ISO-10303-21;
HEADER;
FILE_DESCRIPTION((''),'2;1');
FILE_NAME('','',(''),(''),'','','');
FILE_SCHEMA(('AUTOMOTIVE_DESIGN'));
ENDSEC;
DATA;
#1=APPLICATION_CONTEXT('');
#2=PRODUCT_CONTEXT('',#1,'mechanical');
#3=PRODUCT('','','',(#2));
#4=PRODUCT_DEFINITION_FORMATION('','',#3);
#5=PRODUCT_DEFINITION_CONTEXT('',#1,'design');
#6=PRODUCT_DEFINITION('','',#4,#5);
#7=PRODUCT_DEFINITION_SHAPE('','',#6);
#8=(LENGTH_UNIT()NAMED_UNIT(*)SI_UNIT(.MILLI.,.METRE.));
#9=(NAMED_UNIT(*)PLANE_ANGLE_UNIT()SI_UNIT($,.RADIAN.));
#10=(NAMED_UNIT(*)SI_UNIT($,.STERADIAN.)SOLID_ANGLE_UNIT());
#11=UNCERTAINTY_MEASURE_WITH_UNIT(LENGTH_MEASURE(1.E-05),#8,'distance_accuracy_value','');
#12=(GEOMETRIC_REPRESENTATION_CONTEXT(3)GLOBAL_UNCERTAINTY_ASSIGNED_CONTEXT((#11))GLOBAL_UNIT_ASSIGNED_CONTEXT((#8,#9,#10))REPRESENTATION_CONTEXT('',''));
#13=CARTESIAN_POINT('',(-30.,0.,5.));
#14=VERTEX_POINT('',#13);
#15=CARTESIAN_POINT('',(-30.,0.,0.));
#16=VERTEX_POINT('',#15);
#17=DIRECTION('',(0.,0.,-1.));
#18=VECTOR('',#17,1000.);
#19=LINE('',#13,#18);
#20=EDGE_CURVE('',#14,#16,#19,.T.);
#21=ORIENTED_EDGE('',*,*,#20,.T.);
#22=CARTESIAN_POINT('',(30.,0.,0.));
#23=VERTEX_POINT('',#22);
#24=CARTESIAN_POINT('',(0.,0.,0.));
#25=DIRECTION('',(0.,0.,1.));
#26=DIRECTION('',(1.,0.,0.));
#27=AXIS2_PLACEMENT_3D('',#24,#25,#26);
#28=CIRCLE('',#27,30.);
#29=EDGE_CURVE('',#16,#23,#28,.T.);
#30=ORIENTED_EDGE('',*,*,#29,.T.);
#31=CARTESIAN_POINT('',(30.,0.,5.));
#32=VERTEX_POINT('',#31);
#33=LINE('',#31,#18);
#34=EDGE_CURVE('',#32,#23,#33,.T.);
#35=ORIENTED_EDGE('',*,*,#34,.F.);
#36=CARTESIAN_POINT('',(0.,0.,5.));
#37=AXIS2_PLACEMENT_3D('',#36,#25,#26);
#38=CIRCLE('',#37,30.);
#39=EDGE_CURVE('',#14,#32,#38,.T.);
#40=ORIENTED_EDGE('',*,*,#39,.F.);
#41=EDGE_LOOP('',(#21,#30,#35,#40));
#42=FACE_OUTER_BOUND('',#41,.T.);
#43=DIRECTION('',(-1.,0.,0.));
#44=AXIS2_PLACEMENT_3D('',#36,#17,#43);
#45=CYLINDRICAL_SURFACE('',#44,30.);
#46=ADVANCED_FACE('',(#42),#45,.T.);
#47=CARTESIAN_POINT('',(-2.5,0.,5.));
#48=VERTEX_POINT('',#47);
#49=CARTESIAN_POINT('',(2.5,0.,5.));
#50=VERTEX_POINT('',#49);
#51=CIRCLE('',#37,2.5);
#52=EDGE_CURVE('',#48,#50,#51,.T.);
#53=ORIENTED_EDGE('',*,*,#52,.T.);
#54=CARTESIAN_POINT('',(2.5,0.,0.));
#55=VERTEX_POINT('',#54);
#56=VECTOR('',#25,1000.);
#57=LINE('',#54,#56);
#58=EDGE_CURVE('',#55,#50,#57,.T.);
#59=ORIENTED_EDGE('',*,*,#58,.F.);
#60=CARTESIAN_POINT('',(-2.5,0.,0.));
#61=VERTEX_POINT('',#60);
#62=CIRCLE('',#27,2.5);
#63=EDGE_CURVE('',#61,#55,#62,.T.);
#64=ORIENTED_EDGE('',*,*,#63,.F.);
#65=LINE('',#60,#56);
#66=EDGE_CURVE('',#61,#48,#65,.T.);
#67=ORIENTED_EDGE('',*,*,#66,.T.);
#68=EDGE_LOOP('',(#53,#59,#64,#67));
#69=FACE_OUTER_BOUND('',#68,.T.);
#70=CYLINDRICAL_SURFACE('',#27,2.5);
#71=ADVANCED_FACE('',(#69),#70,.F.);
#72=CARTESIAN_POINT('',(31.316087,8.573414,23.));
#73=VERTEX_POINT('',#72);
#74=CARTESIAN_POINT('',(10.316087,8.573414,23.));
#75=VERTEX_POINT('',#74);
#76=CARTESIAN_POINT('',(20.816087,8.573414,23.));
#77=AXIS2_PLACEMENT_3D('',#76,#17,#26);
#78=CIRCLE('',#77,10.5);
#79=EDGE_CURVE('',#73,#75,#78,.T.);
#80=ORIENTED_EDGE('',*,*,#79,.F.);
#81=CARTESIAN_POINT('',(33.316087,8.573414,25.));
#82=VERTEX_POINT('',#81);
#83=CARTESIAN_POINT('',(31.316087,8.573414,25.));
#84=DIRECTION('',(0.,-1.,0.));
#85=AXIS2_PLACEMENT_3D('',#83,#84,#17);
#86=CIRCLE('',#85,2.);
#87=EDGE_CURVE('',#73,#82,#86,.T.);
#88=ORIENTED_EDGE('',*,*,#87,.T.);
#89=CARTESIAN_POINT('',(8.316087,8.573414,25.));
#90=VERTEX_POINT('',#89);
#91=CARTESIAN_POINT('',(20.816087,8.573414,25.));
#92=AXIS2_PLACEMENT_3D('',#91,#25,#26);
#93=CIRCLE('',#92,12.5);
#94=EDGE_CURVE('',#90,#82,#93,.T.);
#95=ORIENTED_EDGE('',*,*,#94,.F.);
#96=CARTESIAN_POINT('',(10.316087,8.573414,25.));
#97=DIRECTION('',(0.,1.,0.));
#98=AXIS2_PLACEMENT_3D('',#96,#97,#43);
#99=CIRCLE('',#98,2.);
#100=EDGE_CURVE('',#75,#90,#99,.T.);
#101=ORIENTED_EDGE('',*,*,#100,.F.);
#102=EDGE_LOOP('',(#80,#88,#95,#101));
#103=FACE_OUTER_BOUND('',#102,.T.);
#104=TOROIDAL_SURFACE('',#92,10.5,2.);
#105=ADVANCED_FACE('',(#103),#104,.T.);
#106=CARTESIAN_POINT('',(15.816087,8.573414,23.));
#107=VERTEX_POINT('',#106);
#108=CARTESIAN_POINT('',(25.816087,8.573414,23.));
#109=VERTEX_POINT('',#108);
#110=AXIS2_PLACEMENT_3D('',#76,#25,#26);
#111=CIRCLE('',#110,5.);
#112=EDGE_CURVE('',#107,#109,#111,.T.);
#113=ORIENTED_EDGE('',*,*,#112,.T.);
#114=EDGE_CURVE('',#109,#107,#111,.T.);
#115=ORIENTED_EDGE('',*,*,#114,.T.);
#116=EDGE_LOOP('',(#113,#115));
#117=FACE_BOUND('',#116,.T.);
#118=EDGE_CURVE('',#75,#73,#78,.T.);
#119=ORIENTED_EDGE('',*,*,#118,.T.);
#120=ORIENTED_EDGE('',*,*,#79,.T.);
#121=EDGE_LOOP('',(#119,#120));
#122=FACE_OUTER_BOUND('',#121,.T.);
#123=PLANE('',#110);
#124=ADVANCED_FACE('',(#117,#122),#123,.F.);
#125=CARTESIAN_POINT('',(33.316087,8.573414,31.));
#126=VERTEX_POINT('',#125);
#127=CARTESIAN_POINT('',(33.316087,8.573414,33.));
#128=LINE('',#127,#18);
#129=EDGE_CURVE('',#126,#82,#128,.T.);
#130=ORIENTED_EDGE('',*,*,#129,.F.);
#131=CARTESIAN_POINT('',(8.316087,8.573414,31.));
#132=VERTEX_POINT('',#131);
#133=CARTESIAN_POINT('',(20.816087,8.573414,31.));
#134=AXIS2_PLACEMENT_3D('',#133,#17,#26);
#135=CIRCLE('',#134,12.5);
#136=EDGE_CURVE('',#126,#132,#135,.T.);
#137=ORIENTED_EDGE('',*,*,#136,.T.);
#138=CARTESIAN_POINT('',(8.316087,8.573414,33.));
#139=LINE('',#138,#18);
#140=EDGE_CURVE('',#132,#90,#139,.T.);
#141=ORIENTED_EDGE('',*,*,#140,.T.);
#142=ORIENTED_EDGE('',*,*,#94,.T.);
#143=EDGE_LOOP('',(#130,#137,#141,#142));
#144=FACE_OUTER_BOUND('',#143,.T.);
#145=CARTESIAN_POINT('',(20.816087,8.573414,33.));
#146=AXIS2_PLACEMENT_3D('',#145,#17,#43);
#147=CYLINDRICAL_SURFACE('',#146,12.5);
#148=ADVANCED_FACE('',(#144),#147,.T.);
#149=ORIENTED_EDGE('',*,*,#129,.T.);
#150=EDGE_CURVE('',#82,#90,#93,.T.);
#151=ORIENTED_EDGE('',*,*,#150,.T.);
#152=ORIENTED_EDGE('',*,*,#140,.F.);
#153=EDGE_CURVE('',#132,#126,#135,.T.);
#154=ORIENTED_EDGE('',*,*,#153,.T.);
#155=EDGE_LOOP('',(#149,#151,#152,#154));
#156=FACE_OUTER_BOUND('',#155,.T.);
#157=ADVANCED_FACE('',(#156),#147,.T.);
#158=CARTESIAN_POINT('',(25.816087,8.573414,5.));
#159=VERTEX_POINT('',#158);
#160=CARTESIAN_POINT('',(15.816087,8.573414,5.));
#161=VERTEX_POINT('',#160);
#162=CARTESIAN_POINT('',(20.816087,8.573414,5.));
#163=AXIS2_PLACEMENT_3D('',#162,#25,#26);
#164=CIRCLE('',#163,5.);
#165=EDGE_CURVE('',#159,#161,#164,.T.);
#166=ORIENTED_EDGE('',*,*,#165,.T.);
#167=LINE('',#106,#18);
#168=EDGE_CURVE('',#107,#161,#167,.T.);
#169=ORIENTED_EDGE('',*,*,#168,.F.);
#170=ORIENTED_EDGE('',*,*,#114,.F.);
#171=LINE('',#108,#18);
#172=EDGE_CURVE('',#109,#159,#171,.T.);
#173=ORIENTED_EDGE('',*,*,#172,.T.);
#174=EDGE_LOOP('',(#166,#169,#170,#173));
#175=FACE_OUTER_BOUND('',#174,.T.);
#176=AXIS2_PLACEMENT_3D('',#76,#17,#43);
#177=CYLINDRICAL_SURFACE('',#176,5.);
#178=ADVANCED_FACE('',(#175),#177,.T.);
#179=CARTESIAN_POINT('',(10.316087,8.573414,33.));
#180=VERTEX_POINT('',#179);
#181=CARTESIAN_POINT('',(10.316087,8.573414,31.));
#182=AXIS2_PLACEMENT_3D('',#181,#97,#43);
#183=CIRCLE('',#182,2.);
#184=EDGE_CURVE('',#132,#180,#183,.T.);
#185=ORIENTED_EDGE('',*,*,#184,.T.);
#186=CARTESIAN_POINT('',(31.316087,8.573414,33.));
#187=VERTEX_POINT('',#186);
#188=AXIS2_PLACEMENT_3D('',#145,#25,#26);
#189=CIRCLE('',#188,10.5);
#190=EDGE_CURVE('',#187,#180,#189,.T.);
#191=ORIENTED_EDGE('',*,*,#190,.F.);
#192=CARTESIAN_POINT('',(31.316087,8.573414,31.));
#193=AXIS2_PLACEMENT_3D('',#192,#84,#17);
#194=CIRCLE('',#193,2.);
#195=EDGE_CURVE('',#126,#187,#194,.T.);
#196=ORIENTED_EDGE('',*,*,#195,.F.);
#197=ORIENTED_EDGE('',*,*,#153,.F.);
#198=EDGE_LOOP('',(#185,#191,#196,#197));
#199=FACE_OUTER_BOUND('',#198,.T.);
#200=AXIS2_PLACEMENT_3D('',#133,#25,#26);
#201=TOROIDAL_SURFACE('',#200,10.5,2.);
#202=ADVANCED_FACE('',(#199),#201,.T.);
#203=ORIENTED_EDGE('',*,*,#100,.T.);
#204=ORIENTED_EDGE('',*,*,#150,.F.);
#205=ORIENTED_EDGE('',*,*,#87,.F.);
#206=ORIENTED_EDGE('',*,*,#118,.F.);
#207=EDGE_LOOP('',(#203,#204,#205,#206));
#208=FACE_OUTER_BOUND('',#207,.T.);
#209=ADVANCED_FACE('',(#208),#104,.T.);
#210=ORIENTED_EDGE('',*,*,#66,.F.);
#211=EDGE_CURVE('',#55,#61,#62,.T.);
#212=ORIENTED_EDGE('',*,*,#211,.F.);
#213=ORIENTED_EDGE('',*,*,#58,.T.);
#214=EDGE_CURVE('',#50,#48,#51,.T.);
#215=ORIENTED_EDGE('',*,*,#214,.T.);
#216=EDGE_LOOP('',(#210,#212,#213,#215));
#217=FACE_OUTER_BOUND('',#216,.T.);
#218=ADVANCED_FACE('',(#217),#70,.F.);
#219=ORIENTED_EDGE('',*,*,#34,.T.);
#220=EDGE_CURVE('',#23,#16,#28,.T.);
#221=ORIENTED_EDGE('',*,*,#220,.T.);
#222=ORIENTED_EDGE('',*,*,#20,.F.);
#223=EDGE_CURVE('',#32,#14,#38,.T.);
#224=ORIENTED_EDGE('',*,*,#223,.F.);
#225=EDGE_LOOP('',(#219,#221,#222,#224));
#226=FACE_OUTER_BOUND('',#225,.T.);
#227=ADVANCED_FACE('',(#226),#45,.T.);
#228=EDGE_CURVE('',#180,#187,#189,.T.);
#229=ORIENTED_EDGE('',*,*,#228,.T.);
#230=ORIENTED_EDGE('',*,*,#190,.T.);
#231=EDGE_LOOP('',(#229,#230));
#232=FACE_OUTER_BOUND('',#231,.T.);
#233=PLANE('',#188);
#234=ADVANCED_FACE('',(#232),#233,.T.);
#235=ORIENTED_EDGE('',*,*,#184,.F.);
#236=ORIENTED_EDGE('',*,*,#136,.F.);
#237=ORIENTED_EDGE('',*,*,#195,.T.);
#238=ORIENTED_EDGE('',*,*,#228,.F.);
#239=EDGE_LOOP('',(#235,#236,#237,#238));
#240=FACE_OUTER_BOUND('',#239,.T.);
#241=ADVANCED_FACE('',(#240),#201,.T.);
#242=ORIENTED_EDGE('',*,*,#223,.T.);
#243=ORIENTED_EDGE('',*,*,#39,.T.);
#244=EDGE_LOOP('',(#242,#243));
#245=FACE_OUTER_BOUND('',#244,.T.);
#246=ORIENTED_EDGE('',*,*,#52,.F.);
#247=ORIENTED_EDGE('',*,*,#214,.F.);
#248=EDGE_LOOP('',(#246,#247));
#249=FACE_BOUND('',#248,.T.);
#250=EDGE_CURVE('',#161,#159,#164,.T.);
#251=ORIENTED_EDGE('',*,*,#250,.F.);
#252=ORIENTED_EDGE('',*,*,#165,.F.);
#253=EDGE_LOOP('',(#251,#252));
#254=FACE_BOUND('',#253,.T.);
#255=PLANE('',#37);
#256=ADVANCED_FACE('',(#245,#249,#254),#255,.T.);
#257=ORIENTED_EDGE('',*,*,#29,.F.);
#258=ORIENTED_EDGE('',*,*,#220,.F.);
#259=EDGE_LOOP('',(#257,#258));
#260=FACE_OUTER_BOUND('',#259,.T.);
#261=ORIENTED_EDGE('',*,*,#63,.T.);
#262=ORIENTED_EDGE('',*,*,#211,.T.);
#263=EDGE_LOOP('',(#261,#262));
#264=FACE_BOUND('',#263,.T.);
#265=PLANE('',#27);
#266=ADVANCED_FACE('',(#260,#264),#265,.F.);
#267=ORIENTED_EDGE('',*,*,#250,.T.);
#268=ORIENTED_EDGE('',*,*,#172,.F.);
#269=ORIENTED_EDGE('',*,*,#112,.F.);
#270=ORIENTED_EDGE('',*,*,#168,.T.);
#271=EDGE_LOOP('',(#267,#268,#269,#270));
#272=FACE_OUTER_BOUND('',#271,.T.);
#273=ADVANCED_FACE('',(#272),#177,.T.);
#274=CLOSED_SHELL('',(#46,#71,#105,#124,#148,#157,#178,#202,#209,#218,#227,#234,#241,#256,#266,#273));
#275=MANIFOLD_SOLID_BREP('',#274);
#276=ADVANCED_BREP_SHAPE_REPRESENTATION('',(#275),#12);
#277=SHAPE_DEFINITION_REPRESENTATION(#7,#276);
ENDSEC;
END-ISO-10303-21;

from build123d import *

# Parameters (mm, degrees)
SKETCH1_R           = 30
BOSS_EXTRUDE1_DEPTH = 5
SKETCH2_R           = 2.5
CUT_EXTRUDE1_DEPTH  = 5
SKETCH3_R           = 5
BOSS_EXTRUDE2_DEPTH = 18
SKETCH4_R           = 12.5
BOSS_EXTRUDE3_DEPTH = 10
FILLET1_R           = 2


with BuildPart() as part:
    # Sketch1 → Boss-Extrude1 (new body)
    with BuildSketch(Plane.XY):
        Circle(SKETCH1_R)
    extrude(amount=BOSS_EXTRUDE1_DEPTH)

    # Sketch2 → Cut-Extrude1 (cut)
    with BuildSketch(Plane.XY.offset(5)):
        Circle(SKETCH2_R)
    extrude(amount=-CUT_EXTRUDE1_DEPTH, mode=Mode.SUBTRACT)

    # Sketch3 → Boss-Extrude2 (add)
    with BuildSketch(Plane.XY.offset(5)):
        with Locations((20.816087355, 8.573414189)):
            Circle(SKETCH3_R)
    extrude(amount=BOSS_EXTRUDE2_DEPTH)

    # Sketch4 → Boss-Extrude3 (add)
    with BuildSketch(Plane.XY.offset(23)):
        with Locations((20.816087355, 8.573414189)):
            Circle(SKETCH4_R)
    extrude(amount=BOSS_EXTRUDE3_DEPTH)

    # Fillet1
    fillet1_edges = [part.edges().sort_by_distance(p)[0] for p in [
        (8.316087355, 8.573414189, 23),
        (8.316087355, 8.573414189, 33),
    ]]
    fillet(fillet1_edges, radius=FILLET1_R)


solid = part.part
